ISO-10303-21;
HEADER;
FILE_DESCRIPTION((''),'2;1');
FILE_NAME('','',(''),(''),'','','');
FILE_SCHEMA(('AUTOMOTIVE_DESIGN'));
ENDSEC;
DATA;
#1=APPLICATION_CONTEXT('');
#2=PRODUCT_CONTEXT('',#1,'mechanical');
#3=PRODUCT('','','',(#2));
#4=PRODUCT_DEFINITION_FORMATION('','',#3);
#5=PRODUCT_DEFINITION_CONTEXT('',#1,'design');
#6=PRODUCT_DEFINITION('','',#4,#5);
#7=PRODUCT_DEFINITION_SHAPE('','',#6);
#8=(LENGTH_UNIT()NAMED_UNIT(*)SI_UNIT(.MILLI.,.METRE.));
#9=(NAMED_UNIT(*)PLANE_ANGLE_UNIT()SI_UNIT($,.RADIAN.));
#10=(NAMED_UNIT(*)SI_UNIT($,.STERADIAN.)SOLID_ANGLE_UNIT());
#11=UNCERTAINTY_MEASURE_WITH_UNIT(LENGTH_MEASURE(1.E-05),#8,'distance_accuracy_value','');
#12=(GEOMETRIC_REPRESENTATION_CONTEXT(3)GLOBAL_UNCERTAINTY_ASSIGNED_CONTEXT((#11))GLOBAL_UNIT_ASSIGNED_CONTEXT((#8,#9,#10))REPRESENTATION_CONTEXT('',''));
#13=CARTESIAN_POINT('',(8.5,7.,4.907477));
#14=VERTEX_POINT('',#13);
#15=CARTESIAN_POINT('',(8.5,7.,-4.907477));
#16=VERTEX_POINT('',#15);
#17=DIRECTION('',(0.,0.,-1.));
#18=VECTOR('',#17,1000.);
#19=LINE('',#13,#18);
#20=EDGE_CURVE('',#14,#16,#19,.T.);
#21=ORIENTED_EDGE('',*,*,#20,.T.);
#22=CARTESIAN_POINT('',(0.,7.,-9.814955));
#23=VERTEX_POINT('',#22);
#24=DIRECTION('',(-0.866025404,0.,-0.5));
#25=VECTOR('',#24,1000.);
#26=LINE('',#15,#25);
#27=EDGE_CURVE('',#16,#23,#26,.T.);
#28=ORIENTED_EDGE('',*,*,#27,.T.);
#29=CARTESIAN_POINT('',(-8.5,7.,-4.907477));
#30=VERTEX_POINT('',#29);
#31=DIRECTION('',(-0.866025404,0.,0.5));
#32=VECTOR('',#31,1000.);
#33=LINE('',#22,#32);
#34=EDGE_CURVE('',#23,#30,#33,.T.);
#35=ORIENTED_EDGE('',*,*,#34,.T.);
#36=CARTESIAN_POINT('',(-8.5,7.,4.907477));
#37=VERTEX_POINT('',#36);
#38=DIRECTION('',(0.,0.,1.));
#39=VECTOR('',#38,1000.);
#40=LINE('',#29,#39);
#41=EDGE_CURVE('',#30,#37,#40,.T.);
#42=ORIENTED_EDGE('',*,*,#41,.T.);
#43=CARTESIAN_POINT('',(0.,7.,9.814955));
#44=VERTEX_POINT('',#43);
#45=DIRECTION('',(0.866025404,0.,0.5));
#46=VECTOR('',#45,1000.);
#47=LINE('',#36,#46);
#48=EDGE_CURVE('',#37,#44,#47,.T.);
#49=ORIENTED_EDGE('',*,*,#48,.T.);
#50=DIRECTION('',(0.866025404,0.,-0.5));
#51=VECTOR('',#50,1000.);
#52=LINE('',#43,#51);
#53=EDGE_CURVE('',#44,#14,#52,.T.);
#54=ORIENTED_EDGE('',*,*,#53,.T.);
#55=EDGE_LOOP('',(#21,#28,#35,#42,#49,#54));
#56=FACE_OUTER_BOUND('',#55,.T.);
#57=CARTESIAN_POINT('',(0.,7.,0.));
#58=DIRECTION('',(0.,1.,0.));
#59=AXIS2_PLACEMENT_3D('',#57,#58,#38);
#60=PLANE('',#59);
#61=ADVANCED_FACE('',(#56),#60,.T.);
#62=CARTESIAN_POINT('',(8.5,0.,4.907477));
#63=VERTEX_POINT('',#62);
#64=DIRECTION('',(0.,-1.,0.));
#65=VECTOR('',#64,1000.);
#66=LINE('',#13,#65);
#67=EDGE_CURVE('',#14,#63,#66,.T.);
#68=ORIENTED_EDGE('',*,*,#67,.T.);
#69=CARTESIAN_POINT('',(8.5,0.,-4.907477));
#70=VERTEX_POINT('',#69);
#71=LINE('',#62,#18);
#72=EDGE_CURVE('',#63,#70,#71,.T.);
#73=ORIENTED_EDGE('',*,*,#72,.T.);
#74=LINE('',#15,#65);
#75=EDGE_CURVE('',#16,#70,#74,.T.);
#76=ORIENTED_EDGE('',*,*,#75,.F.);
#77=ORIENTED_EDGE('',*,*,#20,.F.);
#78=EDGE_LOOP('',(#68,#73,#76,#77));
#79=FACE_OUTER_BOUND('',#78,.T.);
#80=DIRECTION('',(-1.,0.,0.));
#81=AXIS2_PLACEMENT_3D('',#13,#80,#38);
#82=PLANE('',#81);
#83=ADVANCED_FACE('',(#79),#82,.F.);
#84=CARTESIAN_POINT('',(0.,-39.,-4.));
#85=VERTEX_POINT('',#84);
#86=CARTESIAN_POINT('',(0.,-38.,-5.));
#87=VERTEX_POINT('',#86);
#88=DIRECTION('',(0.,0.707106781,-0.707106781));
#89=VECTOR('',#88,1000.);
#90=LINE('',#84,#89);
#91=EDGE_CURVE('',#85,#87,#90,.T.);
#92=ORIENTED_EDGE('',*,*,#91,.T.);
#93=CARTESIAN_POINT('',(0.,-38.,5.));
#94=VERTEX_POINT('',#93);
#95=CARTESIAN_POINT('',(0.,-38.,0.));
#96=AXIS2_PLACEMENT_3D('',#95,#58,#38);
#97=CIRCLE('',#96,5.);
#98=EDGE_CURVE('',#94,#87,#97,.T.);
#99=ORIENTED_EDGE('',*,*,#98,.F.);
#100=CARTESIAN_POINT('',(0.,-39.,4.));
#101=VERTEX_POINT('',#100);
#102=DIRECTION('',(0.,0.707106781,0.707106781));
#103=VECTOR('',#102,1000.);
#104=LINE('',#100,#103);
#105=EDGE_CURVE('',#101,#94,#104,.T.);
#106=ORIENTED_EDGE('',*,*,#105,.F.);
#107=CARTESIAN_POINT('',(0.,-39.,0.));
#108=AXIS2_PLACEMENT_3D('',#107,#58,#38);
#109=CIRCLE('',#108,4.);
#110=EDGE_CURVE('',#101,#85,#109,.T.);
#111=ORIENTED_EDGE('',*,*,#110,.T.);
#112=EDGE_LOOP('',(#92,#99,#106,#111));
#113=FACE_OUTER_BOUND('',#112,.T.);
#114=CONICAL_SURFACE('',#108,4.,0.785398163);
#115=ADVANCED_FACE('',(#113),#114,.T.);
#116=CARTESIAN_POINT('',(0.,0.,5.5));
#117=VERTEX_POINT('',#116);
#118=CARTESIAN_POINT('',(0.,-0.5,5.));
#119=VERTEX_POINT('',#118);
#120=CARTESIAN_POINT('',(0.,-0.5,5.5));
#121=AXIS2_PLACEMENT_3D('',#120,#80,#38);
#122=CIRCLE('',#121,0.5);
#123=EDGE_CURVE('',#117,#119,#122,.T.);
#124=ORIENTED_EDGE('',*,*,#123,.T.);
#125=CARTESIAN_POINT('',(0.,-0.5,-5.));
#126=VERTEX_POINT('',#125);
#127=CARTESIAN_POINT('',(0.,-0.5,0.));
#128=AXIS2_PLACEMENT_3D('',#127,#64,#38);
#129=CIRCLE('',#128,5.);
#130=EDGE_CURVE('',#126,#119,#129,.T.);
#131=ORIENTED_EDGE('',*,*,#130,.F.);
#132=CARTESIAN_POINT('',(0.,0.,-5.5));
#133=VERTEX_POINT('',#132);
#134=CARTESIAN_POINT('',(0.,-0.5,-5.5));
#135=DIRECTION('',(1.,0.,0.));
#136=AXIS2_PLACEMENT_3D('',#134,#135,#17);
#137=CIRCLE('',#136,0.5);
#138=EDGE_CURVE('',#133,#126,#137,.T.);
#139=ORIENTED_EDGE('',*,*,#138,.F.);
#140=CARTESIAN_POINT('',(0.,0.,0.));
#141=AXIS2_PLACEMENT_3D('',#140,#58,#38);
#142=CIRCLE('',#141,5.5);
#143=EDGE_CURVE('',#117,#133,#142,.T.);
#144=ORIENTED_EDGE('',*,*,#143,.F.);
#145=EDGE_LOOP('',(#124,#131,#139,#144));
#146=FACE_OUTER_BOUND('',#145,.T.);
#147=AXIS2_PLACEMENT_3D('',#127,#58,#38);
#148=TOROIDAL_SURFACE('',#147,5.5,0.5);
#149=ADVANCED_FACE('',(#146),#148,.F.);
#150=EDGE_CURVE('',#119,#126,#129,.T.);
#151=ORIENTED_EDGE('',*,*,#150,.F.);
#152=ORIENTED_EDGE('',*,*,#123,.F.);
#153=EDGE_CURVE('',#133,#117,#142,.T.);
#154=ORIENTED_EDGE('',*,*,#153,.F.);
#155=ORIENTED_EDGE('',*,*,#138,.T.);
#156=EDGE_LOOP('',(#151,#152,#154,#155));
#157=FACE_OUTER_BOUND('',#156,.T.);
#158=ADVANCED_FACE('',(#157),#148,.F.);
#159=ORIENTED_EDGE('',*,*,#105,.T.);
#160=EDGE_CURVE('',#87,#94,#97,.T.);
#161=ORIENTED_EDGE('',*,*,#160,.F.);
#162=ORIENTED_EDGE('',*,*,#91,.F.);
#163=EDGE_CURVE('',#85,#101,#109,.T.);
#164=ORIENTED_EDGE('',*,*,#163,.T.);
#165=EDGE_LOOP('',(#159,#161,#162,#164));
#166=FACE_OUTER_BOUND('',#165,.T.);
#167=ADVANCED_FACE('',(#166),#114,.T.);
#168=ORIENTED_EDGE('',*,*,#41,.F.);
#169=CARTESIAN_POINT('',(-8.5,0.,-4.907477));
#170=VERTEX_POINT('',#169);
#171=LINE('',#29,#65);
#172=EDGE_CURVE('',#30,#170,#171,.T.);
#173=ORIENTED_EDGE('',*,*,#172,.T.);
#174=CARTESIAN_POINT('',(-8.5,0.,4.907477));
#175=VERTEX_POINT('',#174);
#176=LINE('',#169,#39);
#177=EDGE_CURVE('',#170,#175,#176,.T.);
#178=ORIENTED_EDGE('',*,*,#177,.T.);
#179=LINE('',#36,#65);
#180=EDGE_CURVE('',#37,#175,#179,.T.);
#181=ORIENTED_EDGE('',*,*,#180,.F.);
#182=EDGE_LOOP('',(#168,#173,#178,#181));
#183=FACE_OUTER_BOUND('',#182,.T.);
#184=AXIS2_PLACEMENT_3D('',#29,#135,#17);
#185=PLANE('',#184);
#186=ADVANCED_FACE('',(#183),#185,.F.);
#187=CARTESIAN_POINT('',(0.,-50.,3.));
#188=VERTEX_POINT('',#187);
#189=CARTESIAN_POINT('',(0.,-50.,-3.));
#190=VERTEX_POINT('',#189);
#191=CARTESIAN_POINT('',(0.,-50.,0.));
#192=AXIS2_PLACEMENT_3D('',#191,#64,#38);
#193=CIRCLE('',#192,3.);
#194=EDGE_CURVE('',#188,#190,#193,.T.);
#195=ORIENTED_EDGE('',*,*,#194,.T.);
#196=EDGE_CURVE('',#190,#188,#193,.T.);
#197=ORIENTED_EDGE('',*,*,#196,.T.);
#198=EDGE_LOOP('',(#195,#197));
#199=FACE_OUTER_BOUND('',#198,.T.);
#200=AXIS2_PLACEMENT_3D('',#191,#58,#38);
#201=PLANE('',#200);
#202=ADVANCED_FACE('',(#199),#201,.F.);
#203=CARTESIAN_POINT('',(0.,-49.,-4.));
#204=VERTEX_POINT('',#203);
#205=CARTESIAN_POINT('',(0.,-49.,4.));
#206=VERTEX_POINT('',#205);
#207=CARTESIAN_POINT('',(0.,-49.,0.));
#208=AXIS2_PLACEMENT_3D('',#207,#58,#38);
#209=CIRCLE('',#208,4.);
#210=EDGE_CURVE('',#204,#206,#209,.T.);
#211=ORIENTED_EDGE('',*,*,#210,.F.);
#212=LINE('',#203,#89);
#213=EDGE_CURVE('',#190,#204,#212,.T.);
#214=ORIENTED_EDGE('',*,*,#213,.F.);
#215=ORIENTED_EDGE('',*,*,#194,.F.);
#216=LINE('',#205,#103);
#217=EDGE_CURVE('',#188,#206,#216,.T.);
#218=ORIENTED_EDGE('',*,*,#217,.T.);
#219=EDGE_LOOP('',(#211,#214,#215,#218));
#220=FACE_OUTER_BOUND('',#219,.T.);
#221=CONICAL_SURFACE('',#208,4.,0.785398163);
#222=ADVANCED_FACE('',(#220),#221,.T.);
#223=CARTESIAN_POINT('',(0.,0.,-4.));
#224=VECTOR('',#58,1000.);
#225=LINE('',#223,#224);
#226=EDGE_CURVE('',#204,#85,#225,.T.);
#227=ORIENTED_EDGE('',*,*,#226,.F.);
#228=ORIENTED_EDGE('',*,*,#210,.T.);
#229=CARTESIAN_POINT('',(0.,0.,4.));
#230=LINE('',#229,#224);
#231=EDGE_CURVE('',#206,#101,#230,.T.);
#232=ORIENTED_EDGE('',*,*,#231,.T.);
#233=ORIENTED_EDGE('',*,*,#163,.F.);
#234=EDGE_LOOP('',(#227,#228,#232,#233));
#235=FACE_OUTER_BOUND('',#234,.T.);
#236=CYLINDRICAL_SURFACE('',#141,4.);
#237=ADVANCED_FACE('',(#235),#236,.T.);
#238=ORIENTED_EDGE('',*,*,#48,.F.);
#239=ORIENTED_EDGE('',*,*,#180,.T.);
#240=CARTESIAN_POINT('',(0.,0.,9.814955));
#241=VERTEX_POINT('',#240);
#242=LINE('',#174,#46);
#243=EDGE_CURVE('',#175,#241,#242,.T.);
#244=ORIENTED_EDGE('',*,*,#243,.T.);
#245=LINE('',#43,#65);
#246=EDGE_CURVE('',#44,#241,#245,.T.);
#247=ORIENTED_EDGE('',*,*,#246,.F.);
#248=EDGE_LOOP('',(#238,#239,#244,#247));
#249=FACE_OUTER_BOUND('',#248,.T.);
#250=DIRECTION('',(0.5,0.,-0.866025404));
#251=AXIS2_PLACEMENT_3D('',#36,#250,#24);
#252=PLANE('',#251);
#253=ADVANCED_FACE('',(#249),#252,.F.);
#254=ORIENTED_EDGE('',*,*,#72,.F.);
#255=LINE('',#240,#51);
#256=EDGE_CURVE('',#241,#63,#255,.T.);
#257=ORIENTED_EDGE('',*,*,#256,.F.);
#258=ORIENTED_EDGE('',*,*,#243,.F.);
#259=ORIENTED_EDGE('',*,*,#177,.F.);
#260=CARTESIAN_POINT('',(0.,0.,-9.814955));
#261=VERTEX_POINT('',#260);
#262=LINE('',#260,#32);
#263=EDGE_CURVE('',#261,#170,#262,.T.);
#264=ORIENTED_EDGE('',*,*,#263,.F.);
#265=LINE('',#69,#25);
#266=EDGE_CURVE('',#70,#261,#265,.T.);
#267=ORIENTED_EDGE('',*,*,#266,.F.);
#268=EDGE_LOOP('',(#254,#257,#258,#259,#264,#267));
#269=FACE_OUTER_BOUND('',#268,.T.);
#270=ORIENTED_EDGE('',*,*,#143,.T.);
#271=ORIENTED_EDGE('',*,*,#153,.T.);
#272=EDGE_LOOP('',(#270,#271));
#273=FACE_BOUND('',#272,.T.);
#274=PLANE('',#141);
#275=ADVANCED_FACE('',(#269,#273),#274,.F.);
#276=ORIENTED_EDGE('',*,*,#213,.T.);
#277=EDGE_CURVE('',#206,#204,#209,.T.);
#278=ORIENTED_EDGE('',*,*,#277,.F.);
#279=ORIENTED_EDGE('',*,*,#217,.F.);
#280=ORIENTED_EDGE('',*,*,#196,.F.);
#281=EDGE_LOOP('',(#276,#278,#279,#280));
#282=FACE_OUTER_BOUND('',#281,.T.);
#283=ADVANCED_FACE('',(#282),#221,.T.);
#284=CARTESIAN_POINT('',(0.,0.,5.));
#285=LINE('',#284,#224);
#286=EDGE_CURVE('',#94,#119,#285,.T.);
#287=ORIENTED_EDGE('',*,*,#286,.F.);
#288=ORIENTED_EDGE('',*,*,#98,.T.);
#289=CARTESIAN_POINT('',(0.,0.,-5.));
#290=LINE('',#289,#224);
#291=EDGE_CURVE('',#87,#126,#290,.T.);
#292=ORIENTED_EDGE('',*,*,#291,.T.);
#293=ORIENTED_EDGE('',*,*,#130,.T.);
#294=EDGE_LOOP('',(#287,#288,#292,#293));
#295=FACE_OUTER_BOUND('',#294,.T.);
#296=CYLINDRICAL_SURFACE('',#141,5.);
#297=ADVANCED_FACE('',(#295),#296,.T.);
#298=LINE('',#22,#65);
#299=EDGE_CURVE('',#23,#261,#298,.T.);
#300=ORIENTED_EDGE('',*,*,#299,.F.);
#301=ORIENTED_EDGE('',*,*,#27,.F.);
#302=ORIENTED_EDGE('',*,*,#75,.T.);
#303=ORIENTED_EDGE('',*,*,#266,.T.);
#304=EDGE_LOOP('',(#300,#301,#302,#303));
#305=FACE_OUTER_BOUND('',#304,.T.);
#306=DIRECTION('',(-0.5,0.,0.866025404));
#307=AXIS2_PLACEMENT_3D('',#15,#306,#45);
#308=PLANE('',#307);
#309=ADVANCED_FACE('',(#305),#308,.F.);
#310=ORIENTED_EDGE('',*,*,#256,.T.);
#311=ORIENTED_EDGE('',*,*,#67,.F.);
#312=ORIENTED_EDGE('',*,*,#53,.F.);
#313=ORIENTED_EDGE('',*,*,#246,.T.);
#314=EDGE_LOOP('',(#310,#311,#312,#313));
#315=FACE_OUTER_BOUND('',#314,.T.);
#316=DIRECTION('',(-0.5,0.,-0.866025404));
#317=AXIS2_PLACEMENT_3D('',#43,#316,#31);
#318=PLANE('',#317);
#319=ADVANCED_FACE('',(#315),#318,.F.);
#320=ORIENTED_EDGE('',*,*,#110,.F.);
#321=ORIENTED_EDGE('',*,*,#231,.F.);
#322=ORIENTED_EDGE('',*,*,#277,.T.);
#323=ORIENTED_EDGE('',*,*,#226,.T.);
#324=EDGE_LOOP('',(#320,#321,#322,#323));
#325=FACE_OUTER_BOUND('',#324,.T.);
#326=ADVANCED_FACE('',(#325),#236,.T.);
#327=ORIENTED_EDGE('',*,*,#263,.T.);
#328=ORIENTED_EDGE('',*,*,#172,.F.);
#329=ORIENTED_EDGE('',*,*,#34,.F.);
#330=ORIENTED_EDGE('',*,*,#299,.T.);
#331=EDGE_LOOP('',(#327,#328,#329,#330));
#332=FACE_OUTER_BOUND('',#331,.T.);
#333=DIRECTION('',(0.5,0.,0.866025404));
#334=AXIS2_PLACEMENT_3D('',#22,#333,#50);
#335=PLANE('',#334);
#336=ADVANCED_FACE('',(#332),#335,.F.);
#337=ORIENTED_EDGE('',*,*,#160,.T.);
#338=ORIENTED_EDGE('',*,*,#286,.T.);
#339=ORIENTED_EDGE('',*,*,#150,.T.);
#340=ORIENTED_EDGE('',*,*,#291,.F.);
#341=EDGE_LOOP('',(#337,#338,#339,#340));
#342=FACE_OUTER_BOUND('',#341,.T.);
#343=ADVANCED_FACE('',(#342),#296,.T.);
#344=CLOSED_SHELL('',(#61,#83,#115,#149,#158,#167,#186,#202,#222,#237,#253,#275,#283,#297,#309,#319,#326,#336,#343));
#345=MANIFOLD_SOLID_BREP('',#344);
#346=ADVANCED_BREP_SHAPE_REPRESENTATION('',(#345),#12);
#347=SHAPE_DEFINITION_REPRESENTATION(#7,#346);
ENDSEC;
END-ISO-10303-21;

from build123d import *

# Parameters (mm, degrees)
EXTRUDE_1_DEPTH = 7
CHAMFER_1_SIZE  = 1
FILLET_1_R      = 0.5


with BuildPart() as part:
    # 草图1 → 凸台-拉伸1 (new body)
    with BuildSketch(Plane(origin=(0, 0, 0), x_dir=(1, 0, 0), z_dir=(0, 1, 0))):
        Polygon((0, 9.814954576), (-8.5, 4.907477288), (-8.5, -4.907477288), (0, -9.814954576), (8.5, -4.907477288), (8.5, 4.907477288), align=None)
    extrude(amount=EXTRUDE_1_DEPTH)

    # 草图2 → 旋转1 (revolve)
    with BuildSketch(Plane.XY, mode=Mode.PRIVATE) as revolve_1_sk:
        Polygon((0, 0), (0, -50), (4, -50), (4, -39), (5, -38), (5, 0), align=None)
    revolve(revolve_1_sk.sketch.rotate(Axis((0, 0, 0), (0, -1, 0)), 90), axis=Axis((0, 0, 0), (0, -1, 0)))

    # 倒角1
    chamfer_1_edges = [part.edges().sort_by_distance(p)[0] for p in [
        (0, -50, -4),
    ]]
    chamfer(chamfer_1_edges, length=CHAMFER_1_SIZE)

    # 圆角1
    fillet_1_edges = [part.edges().sort_by_distance(p)[0] for p in [
        (0, 0, -5),
    ]]
    fillet(fillet_1_edges, radius=FILLET_1_R)


solid = part.part
